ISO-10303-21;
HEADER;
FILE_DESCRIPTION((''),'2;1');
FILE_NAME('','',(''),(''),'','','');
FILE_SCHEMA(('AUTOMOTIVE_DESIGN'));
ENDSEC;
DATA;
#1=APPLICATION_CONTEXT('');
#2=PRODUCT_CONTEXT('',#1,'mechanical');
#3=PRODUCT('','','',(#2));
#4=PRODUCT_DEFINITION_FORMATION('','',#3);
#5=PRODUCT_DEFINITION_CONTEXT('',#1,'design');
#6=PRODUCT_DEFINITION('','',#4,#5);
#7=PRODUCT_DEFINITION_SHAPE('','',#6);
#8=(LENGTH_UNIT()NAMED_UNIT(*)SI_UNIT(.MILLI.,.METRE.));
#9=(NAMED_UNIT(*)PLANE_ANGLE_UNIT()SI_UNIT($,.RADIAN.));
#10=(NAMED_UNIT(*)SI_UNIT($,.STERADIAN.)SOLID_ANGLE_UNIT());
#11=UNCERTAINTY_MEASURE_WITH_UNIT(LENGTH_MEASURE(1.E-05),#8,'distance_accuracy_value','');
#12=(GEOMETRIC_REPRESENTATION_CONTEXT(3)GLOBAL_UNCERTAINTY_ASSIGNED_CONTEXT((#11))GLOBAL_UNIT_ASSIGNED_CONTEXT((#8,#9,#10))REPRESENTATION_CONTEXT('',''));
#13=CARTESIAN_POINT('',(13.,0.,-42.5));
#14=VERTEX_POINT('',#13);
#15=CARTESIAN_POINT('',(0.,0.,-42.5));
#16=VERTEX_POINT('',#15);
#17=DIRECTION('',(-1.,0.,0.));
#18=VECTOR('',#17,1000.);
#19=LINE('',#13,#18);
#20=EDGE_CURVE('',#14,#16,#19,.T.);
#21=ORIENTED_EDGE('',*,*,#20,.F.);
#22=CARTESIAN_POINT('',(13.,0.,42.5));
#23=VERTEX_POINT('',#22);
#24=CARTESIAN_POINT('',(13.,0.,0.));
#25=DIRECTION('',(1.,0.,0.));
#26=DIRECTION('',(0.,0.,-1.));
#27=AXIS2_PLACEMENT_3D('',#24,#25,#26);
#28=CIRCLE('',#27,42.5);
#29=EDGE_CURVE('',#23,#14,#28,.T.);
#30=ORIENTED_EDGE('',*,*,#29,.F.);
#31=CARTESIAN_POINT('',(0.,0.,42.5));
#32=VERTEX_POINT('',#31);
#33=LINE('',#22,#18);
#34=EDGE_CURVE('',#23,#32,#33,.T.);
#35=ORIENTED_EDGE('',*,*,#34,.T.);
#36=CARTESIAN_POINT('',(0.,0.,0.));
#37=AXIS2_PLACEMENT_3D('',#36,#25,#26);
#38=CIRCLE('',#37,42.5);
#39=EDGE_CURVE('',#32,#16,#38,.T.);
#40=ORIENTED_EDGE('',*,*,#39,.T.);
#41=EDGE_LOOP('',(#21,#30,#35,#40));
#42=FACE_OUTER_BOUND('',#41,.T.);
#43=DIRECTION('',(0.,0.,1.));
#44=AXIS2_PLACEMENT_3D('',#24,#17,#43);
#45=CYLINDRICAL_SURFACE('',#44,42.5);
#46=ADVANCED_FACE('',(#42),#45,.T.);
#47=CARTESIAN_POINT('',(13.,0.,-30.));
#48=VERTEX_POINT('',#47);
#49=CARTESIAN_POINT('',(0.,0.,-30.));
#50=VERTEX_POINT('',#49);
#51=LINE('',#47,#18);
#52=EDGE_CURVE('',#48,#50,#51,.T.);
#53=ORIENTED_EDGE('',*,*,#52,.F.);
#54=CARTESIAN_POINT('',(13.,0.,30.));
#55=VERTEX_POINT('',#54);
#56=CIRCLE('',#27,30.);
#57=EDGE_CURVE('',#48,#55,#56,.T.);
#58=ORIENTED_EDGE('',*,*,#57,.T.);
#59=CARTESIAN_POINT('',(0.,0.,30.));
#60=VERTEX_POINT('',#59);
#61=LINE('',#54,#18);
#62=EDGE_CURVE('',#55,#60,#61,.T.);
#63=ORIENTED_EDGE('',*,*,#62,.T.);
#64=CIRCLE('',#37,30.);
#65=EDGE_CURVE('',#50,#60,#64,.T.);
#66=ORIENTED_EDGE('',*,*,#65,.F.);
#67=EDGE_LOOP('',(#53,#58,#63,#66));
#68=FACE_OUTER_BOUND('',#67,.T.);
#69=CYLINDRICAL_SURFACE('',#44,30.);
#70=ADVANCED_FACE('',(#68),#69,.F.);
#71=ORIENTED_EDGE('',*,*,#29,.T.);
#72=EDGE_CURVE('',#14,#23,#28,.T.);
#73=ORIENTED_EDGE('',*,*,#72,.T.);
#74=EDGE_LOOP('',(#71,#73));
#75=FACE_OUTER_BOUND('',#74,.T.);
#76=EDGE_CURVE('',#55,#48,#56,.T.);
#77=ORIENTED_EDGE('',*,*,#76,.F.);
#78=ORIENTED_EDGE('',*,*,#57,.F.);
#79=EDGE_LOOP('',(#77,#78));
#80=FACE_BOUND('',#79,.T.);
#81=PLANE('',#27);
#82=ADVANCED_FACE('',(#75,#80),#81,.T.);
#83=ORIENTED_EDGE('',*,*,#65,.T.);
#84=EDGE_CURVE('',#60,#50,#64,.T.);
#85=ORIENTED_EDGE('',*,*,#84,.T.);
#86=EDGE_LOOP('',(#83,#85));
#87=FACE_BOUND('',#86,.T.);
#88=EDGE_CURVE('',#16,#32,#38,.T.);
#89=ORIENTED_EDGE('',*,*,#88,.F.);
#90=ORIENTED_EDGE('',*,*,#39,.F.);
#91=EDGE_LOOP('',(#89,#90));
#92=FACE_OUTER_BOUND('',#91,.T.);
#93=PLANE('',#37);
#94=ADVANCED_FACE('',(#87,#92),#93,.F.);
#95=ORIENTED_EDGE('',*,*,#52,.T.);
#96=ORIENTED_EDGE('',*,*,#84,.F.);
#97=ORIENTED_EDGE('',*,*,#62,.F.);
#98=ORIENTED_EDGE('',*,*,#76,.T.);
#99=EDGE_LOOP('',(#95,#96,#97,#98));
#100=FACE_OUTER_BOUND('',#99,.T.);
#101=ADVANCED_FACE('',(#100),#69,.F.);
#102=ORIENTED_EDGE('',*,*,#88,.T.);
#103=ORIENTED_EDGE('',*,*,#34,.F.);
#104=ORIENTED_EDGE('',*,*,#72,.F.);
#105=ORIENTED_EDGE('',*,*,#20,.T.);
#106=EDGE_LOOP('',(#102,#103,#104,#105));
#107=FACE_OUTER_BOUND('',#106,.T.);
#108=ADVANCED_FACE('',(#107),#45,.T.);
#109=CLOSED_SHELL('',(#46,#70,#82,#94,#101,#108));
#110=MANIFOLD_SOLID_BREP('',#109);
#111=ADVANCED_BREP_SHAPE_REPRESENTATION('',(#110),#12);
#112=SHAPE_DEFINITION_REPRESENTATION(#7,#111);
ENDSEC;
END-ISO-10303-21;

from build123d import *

# Parameters (mm, degrees)
SKETCH_1_R      = 42.5
SKETCH_1_R_2    = 30
EXTRUDE_1_DEPTH = 13


with BuildPart() as part:
    # 草图1 → 凸台-拉伸1 (new body)
    with BuildSketch(Plane(origin=(0, 0, 0), x_dir=(0, 0, -1), z_dir=(1, 0, 0))):
        with Locations(Location((0, 0, 0), (0, 0, 180))):
            Circle(SKETCH_1_R)
        with Locations(Location((0, 0, 0), (0, 0, 180))):
            Circle(SKETCH_1_R_2, mode=Mode.SUBTRACT)
    extrude(amount=EXTRUDE_1_DEPTH)


solid = part.part
